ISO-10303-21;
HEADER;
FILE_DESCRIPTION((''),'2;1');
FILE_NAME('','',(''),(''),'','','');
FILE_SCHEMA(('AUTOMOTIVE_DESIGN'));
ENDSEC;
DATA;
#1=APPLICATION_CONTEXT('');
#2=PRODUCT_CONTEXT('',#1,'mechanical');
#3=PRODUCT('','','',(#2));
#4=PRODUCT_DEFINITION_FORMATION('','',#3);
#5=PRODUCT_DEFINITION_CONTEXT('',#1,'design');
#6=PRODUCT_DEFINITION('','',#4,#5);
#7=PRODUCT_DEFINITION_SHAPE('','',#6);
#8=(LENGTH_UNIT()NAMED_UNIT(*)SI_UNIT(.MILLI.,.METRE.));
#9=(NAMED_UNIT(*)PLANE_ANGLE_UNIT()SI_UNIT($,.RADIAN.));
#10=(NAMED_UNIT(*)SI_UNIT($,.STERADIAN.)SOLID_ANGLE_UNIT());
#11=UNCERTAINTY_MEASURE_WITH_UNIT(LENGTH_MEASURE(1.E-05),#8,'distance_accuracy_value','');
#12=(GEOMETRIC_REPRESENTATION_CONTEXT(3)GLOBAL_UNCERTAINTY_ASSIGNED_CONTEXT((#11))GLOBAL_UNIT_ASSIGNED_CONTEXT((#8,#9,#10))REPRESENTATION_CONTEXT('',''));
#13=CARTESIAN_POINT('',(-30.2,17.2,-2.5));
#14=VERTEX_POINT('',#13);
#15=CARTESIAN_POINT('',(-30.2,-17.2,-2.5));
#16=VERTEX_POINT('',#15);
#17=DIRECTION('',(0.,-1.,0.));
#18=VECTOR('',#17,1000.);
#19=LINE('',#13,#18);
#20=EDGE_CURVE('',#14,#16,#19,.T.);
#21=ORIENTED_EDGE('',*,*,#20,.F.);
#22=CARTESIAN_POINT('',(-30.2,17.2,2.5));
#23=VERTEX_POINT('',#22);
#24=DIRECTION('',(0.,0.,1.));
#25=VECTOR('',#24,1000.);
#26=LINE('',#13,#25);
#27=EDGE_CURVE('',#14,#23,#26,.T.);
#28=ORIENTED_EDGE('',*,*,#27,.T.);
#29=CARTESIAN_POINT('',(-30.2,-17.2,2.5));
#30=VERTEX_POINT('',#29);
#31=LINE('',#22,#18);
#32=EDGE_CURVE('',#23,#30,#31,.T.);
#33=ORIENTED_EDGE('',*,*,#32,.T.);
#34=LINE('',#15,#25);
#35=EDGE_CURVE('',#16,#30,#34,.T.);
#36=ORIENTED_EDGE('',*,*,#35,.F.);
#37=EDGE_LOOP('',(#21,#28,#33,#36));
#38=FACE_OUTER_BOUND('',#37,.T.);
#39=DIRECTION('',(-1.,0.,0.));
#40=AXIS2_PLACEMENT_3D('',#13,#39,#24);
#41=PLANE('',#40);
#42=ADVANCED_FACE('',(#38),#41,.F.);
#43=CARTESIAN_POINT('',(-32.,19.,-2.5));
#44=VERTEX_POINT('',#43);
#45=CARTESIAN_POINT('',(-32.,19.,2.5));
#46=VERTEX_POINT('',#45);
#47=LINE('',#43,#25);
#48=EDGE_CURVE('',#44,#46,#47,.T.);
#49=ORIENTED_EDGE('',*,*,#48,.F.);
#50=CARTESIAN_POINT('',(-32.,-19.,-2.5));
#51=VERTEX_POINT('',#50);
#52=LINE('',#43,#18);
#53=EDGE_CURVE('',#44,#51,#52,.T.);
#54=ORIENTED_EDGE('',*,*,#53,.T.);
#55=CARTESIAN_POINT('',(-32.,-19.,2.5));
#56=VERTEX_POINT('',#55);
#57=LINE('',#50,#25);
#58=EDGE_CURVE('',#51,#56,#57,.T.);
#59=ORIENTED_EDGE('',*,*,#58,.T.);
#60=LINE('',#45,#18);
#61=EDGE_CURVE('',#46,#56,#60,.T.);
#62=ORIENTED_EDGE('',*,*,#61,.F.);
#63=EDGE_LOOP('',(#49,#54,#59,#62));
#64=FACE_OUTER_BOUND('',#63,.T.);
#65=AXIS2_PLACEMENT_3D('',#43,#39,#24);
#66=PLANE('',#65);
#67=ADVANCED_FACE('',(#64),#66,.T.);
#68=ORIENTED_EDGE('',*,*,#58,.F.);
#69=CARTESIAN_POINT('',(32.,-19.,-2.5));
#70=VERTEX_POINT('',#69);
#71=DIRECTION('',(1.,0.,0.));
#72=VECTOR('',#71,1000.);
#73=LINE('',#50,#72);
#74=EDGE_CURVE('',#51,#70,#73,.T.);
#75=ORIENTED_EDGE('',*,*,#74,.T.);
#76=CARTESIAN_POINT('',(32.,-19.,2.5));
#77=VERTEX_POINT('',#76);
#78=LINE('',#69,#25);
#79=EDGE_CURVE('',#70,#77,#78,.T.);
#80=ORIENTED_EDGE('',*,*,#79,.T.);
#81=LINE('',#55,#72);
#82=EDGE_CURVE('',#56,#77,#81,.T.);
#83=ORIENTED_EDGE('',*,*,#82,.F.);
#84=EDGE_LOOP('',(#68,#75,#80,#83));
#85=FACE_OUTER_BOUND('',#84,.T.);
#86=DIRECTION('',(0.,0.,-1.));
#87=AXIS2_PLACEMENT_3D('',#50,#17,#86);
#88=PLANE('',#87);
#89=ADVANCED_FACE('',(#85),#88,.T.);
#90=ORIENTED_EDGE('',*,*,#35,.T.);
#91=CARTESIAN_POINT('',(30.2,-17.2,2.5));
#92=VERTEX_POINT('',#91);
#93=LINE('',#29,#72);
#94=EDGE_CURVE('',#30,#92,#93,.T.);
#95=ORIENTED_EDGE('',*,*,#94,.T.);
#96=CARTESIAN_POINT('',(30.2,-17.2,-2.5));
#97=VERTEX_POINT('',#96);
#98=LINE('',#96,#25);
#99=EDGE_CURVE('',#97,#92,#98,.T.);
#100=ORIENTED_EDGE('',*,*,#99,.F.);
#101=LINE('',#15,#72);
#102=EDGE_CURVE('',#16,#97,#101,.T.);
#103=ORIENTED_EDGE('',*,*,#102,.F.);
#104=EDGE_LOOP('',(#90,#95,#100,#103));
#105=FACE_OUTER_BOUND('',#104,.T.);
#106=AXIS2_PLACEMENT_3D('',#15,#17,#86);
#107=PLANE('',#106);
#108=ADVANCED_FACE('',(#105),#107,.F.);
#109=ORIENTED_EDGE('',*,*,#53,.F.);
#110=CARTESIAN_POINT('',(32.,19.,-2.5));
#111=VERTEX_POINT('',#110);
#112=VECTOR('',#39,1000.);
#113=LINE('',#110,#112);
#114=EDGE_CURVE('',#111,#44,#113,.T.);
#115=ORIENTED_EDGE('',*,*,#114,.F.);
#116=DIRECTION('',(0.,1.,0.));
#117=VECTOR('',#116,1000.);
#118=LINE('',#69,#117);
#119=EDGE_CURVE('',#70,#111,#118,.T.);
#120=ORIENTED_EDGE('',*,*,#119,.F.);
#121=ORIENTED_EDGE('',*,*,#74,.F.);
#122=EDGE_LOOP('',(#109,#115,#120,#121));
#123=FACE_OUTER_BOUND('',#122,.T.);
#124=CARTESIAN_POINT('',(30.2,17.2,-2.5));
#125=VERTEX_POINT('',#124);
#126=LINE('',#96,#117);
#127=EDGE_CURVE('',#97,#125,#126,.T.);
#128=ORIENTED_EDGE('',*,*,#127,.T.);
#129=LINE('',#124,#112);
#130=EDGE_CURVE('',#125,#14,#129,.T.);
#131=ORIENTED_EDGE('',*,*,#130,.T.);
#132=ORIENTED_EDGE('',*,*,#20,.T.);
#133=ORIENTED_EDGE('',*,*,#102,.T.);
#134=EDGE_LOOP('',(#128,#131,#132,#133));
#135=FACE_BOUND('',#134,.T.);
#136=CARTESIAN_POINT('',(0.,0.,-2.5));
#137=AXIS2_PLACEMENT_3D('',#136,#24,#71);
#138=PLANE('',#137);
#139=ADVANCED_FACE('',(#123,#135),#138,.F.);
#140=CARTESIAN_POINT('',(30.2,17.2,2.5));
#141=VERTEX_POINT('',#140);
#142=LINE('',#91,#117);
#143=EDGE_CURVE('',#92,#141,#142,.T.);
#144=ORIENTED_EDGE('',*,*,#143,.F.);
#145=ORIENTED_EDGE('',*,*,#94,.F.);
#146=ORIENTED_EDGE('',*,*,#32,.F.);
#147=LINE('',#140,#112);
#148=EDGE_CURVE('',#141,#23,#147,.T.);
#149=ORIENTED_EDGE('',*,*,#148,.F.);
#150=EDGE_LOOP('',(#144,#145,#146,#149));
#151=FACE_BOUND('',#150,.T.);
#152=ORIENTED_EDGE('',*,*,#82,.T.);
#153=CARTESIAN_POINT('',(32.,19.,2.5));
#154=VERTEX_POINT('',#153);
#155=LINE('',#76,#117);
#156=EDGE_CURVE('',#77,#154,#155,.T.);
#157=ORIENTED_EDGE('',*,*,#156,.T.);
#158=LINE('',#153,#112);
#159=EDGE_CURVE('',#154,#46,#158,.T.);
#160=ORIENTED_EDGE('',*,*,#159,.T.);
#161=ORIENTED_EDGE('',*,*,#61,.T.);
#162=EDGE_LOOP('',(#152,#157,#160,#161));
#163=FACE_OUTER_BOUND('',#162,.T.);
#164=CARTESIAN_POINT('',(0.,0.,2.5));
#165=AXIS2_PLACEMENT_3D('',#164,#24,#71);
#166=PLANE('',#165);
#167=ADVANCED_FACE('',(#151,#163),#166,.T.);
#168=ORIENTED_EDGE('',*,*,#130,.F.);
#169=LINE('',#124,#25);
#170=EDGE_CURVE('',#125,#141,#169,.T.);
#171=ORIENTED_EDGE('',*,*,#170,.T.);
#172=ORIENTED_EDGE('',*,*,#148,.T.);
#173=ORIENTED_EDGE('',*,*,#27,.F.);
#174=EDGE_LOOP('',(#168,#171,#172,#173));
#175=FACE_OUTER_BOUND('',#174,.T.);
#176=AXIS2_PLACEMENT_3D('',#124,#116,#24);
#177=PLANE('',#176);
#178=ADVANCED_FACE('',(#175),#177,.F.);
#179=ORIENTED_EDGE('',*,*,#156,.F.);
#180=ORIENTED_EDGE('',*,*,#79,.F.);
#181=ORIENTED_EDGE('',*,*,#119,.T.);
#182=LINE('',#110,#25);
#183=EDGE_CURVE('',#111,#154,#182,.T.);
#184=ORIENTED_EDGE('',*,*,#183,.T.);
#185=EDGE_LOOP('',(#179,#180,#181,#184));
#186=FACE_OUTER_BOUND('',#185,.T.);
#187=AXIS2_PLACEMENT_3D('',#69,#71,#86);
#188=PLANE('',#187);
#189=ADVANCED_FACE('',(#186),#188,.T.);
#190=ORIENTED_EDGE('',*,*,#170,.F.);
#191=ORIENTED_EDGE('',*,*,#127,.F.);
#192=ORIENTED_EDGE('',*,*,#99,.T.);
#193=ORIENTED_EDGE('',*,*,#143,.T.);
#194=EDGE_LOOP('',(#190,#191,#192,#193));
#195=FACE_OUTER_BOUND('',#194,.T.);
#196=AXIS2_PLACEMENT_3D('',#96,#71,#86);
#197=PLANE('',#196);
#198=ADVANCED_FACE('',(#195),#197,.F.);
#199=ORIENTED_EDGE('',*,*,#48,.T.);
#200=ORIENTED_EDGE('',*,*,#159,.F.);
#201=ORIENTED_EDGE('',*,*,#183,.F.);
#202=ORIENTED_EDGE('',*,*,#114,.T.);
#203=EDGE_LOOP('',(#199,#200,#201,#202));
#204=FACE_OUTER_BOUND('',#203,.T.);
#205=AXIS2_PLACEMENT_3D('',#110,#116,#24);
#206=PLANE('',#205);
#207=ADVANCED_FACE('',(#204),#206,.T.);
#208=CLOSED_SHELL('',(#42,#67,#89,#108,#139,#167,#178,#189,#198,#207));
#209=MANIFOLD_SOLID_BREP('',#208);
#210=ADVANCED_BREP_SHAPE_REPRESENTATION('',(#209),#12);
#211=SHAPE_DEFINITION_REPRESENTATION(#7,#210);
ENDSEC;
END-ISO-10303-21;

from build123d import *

# Parameters (mm, degrees)
SKETCH_1_W      = 64
SKETCH_1_H      = 38
SKETCH_1_W_2    = 60.4
SKETCH_1_H_2    = 34.4
EXTRUDE_1_DEPTH = 2.5


with BuildPart() as part:
    # 草图1 → 凸台-拉伸1 (new, symmetric)
    with BuildSketch(Plane.XY):
        Rectangle(SKETCH_1_W, SKETCH_1_H)
        Rectangle(SKETCH_1_W_2, SKETCH_1_H_2, mode=Mode.SUBTRACT)
    extrude(amount=EXTRUDE_1_DEPTH, both=True)


solid = part.part
